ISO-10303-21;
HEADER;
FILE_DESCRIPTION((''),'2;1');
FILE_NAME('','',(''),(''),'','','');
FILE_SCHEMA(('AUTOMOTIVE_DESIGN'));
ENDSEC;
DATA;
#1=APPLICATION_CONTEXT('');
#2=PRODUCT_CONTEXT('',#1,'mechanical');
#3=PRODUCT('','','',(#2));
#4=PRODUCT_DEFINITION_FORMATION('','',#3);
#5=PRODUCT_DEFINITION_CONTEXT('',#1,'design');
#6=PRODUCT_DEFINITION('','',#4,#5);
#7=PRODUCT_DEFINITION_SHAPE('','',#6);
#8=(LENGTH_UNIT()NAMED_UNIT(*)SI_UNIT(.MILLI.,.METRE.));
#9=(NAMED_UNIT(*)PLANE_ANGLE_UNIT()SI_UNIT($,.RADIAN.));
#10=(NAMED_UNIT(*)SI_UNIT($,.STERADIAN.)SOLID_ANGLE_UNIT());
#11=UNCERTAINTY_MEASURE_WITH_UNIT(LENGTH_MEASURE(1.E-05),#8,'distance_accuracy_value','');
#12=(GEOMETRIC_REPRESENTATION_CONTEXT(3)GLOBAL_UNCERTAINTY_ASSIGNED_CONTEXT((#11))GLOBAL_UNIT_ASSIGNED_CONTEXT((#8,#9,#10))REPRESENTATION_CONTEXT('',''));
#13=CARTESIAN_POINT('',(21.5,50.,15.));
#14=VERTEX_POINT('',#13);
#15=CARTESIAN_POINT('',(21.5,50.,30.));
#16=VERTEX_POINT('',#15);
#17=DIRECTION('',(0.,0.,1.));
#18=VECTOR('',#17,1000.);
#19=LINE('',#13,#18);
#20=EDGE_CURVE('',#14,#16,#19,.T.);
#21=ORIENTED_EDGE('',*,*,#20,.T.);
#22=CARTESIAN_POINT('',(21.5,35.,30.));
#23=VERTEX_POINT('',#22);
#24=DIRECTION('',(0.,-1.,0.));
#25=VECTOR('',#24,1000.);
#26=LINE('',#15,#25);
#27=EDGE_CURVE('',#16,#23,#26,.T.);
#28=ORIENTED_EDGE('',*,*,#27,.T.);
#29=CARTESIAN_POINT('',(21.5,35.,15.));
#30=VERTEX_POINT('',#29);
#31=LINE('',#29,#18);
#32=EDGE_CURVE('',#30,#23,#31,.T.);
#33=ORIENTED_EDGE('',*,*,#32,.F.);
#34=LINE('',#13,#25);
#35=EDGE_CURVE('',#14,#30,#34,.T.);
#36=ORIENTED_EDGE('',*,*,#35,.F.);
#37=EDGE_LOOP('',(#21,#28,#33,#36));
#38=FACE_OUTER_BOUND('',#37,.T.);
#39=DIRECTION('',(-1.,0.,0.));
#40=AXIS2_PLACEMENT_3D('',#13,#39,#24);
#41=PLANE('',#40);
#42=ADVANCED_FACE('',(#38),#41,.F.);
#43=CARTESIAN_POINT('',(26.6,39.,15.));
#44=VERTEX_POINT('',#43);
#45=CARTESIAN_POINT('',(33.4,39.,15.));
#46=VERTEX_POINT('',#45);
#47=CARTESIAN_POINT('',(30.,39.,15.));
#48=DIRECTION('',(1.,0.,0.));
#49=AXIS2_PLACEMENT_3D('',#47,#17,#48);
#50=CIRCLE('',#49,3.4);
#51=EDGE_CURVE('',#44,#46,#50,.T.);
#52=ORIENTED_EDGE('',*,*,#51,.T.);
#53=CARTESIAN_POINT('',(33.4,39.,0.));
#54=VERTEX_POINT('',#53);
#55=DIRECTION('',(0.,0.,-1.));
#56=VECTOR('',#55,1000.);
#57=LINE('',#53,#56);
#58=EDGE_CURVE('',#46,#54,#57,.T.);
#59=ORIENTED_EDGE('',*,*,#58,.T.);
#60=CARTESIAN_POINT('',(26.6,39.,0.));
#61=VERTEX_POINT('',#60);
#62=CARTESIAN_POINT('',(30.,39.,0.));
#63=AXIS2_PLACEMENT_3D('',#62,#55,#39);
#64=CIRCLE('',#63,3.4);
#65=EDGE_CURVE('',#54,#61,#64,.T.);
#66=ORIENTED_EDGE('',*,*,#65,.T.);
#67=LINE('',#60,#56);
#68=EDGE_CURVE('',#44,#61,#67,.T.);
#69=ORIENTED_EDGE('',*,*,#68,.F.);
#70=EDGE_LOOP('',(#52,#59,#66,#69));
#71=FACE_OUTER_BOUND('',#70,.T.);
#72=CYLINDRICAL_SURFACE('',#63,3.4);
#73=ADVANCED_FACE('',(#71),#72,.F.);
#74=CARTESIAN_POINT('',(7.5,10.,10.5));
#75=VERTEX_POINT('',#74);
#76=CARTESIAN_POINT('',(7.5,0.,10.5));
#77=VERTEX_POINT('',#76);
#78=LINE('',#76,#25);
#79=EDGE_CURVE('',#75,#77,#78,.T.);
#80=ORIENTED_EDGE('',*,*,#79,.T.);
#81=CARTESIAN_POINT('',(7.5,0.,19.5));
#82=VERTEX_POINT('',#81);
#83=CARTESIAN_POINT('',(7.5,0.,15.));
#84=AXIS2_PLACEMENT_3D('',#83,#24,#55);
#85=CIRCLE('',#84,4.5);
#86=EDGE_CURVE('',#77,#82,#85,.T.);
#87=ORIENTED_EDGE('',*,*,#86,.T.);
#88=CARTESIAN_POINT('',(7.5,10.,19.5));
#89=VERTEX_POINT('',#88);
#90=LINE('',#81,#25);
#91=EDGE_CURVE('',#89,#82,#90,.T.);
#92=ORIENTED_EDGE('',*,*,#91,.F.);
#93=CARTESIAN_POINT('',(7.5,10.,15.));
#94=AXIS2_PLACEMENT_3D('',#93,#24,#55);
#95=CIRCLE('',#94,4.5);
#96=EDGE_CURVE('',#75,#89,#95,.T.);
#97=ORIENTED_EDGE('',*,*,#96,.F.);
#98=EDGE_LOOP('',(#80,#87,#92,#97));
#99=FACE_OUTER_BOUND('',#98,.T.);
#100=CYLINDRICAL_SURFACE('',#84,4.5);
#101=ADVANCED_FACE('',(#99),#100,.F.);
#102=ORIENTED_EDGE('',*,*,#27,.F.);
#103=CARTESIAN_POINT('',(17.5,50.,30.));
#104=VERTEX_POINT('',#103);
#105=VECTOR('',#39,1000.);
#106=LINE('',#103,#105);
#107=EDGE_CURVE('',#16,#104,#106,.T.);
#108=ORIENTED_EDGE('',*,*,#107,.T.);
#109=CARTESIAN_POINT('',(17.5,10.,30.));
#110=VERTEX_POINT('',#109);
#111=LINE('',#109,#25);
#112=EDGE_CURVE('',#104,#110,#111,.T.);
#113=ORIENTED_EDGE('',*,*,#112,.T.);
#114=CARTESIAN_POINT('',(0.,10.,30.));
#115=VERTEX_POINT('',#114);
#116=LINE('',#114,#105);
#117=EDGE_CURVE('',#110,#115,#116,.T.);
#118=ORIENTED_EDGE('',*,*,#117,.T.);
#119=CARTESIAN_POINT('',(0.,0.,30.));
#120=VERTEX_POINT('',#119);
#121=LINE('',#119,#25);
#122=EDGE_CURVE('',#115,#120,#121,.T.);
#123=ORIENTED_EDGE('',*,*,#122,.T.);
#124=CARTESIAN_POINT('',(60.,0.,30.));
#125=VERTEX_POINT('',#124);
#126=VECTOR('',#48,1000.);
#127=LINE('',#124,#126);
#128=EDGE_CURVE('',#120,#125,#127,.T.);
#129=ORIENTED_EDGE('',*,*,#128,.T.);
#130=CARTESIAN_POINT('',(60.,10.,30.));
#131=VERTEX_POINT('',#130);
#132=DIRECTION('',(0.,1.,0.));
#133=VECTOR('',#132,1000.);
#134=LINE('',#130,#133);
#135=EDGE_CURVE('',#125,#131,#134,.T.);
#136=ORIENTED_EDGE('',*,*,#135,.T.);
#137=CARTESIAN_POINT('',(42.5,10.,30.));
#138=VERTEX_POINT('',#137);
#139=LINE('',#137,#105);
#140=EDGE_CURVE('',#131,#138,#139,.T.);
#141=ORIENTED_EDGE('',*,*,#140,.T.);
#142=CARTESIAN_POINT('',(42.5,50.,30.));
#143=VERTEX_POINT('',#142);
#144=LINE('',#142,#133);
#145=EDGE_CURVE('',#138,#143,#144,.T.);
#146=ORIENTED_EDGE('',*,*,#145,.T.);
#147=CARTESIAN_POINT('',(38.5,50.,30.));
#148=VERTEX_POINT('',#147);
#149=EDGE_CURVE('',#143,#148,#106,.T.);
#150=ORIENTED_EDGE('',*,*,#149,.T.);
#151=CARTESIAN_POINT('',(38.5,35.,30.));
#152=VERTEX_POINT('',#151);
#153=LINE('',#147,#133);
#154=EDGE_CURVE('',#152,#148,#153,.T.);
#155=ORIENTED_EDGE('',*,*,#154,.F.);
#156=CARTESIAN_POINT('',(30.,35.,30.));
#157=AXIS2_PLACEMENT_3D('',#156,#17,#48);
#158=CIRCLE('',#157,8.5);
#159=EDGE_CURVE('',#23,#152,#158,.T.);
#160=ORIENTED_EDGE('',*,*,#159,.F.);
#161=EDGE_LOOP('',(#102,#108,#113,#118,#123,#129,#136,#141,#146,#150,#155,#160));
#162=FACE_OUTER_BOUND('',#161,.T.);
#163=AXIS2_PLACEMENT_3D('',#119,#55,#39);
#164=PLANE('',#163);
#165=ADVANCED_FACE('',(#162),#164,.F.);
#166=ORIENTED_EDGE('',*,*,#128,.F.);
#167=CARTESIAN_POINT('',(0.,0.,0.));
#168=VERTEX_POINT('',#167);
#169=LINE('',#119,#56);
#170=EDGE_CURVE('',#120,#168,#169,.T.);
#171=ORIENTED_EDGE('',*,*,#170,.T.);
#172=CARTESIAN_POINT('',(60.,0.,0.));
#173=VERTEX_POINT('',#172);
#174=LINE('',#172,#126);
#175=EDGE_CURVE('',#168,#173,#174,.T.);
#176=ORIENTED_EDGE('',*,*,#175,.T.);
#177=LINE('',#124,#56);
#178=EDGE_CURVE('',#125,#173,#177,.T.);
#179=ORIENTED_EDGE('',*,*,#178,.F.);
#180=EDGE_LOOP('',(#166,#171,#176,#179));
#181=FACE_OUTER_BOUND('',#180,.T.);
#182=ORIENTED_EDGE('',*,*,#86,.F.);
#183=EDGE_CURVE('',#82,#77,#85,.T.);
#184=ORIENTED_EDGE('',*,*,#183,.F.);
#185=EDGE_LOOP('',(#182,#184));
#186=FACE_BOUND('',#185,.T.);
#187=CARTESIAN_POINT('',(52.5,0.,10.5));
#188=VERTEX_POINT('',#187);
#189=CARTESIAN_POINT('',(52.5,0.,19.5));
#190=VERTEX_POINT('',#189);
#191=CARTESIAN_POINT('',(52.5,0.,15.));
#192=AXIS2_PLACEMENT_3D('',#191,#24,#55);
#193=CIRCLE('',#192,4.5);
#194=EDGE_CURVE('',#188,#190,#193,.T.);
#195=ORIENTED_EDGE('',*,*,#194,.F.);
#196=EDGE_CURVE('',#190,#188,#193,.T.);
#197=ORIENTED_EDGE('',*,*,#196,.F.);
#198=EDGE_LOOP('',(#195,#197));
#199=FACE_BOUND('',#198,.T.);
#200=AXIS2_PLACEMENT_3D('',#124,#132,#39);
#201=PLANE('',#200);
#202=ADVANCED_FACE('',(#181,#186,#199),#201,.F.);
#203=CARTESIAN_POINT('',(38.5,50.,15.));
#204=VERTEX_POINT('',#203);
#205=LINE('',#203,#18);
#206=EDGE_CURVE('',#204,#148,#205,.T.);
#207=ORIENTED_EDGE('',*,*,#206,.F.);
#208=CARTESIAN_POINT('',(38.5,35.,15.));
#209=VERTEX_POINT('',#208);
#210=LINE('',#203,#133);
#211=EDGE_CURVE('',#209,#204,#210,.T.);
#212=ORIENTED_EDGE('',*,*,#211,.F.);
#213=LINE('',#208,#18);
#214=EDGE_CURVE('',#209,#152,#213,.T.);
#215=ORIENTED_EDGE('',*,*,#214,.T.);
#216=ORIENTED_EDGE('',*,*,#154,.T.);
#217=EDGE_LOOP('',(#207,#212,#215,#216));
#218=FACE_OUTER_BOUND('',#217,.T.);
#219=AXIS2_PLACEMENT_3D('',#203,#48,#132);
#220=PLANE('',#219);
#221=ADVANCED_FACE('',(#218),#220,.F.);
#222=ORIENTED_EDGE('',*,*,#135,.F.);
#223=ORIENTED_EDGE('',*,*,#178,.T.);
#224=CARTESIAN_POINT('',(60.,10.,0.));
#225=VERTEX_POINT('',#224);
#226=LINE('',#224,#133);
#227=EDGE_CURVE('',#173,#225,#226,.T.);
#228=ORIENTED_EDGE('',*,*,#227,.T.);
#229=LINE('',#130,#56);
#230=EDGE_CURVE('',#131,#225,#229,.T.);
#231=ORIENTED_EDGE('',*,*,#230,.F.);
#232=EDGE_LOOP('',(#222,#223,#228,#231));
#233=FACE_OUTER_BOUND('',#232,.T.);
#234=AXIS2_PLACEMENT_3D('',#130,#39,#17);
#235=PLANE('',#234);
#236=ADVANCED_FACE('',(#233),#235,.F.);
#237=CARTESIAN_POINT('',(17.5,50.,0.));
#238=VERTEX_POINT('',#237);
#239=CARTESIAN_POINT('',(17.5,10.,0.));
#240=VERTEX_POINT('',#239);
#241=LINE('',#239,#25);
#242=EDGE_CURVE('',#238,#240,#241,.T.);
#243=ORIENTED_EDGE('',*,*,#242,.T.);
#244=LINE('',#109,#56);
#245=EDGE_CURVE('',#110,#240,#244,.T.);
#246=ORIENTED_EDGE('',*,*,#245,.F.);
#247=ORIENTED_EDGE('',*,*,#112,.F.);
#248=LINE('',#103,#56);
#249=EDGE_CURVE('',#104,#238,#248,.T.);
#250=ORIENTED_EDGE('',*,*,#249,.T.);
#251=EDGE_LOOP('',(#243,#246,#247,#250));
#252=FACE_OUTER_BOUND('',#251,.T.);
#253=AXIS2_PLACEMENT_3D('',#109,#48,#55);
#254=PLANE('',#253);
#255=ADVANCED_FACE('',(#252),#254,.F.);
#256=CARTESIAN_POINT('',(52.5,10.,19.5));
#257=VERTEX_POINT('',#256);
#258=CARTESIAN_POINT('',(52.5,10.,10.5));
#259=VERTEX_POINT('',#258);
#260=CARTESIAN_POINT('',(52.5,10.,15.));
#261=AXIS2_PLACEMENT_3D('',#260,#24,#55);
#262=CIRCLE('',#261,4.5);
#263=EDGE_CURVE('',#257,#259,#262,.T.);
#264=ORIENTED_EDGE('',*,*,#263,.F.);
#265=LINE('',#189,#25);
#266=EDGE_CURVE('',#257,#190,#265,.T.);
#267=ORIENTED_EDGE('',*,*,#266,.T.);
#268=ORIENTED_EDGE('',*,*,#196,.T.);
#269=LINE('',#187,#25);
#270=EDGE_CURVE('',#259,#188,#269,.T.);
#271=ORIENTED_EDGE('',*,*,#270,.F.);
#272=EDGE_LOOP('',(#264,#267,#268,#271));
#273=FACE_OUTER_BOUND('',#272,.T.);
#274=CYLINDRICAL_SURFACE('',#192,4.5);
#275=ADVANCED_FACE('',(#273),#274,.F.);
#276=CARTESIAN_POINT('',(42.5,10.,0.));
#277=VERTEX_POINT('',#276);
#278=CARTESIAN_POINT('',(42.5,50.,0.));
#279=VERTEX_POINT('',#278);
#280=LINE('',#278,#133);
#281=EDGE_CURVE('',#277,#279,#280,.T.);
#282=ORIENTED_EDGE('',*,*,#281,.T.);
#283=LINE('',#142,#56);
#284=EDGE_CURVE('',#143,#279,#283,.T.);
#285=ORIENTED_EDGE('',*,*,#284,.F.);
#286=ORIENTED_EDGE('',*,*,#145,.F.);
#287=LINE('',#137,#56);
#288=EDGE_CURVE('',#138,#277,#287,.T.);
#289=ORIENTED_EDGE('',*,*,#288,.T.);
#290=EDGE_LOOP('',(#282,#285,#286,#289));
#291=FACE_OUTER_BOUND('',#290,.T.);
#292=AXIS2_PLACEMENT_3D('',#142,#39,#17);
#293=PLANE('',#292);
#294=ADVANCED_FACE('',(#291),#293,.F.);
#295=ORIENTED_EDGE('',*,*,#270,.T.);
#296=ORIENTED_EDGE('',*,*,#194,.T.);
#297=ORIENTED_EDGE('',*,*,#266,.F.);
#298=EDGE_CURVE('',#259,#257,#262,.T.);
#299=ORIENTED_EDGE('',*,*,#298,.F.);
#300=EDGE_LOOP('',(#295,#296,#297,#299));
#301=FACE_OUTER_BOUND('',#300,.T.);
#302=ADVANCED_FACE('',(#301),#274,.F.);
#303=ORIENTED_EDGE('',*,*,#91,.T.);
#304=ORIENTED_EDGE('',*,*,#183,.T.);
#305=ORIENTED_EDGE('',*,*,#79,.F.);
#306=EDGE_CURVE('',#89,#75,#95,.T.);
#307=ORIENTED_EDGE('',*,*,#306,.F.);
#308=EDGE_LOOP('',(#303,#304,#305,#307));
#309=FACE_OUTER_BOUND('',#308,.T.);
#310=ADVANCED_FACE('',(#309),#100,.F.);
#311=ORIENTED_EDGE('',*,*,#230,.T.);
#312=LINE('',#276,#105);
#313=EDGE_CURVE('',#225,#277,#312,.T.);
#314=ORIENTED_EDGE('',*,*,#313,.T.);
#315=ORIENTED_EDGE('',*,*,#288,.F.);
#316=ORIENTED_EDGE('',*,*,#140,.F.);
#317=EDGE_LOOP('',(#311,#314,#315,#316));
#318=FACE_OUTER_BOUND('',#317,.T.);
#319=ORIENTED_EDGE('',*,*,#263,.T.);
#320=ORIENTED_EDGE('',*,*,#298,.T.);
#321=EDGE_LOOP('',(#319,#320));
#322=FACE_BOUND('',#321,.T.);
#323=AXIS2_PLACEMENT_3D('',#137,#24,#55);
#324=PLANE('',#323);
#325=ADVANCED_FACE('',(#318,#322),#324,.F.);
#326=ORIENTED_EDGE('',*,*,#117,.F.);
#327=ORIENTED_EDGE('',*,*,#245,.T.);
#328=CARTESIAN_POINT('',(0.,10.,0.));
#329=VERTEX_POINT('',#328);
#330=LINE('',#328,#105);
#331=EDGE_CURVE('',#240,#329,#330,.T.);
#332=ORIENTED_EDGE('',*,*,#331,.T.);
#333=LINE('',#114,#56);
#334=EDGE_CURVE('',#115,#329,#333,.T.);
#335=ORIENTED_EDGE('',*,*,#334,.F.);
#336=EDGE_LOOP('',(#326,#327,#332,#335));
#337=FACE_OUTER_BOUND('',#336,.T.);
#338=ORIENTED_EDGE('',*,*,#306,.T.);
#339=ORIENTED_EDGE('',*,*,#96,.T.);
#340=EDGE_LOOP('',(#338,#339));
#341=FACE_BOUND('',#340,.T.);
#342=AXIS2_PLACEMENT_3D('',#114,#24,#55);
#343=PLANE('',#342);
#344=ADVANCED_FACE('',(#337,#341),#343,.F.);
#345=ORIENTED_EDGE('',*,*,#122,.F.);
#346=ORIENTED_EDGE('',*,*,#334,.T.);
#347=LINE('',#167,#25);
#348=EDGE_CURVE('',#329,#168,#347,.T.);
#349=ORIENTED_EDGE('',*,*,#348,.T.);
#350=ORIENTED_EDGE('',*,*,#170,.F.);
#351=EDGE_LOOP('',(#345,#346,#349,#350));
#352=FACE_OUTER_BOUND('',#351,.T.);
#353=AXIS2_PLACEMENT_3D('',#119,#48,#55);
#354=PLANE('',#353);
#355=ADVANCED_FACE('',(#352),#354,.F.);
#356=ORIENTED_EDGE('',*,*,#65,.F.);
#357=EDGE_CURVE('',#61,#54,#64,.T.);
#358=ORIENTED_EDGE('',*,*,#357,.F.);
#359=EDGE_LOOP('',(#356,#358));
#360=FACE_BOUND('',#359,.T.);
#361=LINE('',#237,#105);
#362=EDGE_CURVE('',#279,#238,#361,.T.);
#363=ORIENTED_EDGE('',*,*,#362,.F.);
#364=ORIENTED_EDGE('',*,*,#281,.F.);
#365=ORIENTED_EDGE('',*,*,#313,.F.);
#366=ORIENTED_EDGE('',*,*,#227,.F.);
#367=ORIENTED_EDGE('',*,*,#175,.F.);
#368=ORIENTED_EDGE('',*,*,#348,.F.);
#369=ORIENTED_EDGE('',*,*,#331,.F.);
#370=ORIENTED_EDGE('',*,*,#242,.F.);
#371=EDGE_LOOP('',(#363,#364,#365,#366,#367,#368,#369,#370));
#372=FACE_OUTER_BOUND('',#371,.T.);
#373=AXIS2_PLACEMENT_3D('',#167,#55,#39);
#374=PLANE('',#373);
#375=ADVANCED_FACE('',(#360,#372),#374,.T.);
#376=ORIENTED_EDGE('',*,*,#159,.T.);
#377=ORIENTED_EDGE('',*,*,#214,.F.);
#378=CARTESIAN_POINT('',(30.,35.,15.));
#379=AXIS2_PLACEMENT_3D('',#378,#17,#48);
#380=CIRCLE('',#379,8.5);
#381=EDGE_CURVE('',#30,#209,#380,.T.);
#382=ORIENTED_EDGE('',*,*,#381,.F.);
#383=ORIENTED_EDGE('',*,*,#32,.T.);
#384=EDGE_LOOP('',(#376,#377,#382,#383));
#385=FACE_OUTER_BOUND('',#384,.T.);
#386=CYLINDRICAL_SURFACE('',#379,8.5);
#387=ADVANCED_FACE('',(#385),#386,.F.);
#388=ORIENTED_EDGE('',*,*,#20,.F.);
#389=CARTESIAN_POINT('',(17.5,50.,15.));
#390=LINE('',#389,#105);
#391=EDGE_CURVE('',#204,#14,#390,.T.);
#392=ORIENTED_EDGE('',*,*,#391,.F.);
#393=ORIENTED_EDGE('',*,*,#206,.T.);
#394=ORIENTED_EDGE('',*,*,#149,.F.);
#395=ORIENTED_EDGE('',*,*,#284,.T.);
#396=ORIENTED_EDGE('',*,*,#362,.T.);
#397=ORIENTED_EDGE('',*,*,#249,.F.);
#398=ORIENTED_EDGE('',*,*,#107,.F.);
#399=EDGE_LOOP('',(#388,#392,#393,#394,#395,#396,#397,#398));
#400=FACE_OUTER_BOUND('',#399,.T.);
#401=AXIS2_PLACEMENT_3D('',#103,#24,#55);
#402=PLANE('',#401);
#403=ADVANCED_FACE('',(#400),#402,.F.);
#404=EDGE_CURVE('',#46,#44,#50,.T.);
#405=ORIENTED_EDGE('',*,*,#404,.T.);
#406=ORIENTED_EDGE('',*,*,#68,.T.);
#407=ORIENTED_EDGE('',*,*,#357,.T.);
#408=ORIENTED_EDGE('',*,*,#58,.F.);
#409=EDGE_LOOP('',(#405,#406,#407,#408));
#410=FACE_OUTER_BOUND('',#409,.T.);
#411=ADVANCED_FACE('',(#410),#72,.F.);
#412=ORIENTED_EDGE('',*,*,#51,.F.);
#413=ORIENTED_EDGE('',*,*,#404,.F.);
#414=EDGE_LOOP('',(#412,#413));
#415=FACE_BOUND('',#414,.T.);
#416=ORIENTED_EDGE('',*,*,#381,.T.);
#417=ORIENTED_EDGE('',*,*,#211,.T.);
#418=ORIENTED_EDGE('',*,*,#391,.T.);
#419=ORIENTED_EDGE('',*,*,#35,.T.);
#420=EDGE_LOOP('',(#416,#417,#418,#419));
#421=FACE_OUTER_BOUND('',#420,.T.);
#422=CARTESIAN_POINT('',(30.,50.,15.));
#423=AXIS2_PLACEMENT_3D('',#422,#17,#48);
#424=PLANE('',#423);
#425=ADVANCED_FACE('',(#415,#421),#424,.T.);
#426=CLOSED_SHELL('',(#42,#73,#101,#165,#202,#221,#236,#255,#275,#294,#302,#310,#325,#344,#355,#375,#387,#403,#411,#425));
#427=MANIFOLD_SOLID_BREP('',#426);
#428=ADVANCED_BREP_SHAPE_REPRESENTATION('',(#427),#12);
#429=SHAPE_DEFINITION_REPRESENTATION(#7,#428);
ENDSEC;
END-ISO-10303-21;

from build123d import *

# Parameters (mm, degrees)
BOSS_EXTRUDE1_DEPTH          = 30
CUT_EXTRUDE1_DEPTH           = 15
F_9_0_9_DIAMETER_HOLE1_D     = 9
F_9_0_9_DIAMETER_HOLE1_DEPTH = 10
F_9_0_9_DIAMETER_HOLE1_TIP   = 2.703872786
M8_TAPPED_HOLE1_D            = 6.8


with BuildPart() as part:
    # Sketch1 → Boss-Extrude1 (new body)
    with BuildSketch(Plane.XY):
        Polygon((0, 0), (0, 10), (17.5, 10), (17.5, 50), (42.5, 50), (42.5, 10), (60, 10), (60, 0), align=None)
    extrude(amount=BOSS_EXTRUDE1_DEPTH)

    # Sketch2 → Cut-Extrude1 (cut)
    with BuildSketch(Plane.XY.offset(30)):
        with BuildLine():
            Line((38.5, 50), (38.5, 35))
            ThreePointArc((38.5, 35), (30, 26.5), (21.5, 35))
            Line((21.5, 35), (21.5, 50))
            ThreePointArc((21.5, 50), (30, 58.5), (38.5, 50))
        make_face()
    extrude(amount=-CUT_EXTRUDE1_DEPTH, mode=Mode.SUBTRACT)

    # Ø9.0 (9) Diameter Hole1
    with Locations(Plane(origin=(7.5, 0, 15), x_dir=(-1, 0, 0), z_dir=(0, -1, 0))):
        with Locations((0, 0), (-45, 0)):
            Hole(F_9_0_9_DIAMETER_HOLE1_D / 2, depth=F_9_0_9_DIAMETER_HOLE1_DEPTH)
            with Locations((0, 0, -(F_9_0_9_DIAMETER_HOLE1_DEPTH + F_9_0_9_DIAMETER_HOLE1_TIP / 2))):  # 118° drill point
                Cone(0, F_9_0_9_DIAMETER_HOLE1_D / 2, F_9_0_9_DIAMETER_HOLE1_TIP, mode=Mode.SUBTRACT)

    # M8 Tapped Hole1 (through all)
    with Locations(Plane(origin=(30, 39, 0), x_dir=(-1, 0, 0), z_dir=(0, 0, -1))):
        with Locations((0, 0)):
            Hole(M8_TAPPED_HOLE1_D / 2)


solid = part.part
